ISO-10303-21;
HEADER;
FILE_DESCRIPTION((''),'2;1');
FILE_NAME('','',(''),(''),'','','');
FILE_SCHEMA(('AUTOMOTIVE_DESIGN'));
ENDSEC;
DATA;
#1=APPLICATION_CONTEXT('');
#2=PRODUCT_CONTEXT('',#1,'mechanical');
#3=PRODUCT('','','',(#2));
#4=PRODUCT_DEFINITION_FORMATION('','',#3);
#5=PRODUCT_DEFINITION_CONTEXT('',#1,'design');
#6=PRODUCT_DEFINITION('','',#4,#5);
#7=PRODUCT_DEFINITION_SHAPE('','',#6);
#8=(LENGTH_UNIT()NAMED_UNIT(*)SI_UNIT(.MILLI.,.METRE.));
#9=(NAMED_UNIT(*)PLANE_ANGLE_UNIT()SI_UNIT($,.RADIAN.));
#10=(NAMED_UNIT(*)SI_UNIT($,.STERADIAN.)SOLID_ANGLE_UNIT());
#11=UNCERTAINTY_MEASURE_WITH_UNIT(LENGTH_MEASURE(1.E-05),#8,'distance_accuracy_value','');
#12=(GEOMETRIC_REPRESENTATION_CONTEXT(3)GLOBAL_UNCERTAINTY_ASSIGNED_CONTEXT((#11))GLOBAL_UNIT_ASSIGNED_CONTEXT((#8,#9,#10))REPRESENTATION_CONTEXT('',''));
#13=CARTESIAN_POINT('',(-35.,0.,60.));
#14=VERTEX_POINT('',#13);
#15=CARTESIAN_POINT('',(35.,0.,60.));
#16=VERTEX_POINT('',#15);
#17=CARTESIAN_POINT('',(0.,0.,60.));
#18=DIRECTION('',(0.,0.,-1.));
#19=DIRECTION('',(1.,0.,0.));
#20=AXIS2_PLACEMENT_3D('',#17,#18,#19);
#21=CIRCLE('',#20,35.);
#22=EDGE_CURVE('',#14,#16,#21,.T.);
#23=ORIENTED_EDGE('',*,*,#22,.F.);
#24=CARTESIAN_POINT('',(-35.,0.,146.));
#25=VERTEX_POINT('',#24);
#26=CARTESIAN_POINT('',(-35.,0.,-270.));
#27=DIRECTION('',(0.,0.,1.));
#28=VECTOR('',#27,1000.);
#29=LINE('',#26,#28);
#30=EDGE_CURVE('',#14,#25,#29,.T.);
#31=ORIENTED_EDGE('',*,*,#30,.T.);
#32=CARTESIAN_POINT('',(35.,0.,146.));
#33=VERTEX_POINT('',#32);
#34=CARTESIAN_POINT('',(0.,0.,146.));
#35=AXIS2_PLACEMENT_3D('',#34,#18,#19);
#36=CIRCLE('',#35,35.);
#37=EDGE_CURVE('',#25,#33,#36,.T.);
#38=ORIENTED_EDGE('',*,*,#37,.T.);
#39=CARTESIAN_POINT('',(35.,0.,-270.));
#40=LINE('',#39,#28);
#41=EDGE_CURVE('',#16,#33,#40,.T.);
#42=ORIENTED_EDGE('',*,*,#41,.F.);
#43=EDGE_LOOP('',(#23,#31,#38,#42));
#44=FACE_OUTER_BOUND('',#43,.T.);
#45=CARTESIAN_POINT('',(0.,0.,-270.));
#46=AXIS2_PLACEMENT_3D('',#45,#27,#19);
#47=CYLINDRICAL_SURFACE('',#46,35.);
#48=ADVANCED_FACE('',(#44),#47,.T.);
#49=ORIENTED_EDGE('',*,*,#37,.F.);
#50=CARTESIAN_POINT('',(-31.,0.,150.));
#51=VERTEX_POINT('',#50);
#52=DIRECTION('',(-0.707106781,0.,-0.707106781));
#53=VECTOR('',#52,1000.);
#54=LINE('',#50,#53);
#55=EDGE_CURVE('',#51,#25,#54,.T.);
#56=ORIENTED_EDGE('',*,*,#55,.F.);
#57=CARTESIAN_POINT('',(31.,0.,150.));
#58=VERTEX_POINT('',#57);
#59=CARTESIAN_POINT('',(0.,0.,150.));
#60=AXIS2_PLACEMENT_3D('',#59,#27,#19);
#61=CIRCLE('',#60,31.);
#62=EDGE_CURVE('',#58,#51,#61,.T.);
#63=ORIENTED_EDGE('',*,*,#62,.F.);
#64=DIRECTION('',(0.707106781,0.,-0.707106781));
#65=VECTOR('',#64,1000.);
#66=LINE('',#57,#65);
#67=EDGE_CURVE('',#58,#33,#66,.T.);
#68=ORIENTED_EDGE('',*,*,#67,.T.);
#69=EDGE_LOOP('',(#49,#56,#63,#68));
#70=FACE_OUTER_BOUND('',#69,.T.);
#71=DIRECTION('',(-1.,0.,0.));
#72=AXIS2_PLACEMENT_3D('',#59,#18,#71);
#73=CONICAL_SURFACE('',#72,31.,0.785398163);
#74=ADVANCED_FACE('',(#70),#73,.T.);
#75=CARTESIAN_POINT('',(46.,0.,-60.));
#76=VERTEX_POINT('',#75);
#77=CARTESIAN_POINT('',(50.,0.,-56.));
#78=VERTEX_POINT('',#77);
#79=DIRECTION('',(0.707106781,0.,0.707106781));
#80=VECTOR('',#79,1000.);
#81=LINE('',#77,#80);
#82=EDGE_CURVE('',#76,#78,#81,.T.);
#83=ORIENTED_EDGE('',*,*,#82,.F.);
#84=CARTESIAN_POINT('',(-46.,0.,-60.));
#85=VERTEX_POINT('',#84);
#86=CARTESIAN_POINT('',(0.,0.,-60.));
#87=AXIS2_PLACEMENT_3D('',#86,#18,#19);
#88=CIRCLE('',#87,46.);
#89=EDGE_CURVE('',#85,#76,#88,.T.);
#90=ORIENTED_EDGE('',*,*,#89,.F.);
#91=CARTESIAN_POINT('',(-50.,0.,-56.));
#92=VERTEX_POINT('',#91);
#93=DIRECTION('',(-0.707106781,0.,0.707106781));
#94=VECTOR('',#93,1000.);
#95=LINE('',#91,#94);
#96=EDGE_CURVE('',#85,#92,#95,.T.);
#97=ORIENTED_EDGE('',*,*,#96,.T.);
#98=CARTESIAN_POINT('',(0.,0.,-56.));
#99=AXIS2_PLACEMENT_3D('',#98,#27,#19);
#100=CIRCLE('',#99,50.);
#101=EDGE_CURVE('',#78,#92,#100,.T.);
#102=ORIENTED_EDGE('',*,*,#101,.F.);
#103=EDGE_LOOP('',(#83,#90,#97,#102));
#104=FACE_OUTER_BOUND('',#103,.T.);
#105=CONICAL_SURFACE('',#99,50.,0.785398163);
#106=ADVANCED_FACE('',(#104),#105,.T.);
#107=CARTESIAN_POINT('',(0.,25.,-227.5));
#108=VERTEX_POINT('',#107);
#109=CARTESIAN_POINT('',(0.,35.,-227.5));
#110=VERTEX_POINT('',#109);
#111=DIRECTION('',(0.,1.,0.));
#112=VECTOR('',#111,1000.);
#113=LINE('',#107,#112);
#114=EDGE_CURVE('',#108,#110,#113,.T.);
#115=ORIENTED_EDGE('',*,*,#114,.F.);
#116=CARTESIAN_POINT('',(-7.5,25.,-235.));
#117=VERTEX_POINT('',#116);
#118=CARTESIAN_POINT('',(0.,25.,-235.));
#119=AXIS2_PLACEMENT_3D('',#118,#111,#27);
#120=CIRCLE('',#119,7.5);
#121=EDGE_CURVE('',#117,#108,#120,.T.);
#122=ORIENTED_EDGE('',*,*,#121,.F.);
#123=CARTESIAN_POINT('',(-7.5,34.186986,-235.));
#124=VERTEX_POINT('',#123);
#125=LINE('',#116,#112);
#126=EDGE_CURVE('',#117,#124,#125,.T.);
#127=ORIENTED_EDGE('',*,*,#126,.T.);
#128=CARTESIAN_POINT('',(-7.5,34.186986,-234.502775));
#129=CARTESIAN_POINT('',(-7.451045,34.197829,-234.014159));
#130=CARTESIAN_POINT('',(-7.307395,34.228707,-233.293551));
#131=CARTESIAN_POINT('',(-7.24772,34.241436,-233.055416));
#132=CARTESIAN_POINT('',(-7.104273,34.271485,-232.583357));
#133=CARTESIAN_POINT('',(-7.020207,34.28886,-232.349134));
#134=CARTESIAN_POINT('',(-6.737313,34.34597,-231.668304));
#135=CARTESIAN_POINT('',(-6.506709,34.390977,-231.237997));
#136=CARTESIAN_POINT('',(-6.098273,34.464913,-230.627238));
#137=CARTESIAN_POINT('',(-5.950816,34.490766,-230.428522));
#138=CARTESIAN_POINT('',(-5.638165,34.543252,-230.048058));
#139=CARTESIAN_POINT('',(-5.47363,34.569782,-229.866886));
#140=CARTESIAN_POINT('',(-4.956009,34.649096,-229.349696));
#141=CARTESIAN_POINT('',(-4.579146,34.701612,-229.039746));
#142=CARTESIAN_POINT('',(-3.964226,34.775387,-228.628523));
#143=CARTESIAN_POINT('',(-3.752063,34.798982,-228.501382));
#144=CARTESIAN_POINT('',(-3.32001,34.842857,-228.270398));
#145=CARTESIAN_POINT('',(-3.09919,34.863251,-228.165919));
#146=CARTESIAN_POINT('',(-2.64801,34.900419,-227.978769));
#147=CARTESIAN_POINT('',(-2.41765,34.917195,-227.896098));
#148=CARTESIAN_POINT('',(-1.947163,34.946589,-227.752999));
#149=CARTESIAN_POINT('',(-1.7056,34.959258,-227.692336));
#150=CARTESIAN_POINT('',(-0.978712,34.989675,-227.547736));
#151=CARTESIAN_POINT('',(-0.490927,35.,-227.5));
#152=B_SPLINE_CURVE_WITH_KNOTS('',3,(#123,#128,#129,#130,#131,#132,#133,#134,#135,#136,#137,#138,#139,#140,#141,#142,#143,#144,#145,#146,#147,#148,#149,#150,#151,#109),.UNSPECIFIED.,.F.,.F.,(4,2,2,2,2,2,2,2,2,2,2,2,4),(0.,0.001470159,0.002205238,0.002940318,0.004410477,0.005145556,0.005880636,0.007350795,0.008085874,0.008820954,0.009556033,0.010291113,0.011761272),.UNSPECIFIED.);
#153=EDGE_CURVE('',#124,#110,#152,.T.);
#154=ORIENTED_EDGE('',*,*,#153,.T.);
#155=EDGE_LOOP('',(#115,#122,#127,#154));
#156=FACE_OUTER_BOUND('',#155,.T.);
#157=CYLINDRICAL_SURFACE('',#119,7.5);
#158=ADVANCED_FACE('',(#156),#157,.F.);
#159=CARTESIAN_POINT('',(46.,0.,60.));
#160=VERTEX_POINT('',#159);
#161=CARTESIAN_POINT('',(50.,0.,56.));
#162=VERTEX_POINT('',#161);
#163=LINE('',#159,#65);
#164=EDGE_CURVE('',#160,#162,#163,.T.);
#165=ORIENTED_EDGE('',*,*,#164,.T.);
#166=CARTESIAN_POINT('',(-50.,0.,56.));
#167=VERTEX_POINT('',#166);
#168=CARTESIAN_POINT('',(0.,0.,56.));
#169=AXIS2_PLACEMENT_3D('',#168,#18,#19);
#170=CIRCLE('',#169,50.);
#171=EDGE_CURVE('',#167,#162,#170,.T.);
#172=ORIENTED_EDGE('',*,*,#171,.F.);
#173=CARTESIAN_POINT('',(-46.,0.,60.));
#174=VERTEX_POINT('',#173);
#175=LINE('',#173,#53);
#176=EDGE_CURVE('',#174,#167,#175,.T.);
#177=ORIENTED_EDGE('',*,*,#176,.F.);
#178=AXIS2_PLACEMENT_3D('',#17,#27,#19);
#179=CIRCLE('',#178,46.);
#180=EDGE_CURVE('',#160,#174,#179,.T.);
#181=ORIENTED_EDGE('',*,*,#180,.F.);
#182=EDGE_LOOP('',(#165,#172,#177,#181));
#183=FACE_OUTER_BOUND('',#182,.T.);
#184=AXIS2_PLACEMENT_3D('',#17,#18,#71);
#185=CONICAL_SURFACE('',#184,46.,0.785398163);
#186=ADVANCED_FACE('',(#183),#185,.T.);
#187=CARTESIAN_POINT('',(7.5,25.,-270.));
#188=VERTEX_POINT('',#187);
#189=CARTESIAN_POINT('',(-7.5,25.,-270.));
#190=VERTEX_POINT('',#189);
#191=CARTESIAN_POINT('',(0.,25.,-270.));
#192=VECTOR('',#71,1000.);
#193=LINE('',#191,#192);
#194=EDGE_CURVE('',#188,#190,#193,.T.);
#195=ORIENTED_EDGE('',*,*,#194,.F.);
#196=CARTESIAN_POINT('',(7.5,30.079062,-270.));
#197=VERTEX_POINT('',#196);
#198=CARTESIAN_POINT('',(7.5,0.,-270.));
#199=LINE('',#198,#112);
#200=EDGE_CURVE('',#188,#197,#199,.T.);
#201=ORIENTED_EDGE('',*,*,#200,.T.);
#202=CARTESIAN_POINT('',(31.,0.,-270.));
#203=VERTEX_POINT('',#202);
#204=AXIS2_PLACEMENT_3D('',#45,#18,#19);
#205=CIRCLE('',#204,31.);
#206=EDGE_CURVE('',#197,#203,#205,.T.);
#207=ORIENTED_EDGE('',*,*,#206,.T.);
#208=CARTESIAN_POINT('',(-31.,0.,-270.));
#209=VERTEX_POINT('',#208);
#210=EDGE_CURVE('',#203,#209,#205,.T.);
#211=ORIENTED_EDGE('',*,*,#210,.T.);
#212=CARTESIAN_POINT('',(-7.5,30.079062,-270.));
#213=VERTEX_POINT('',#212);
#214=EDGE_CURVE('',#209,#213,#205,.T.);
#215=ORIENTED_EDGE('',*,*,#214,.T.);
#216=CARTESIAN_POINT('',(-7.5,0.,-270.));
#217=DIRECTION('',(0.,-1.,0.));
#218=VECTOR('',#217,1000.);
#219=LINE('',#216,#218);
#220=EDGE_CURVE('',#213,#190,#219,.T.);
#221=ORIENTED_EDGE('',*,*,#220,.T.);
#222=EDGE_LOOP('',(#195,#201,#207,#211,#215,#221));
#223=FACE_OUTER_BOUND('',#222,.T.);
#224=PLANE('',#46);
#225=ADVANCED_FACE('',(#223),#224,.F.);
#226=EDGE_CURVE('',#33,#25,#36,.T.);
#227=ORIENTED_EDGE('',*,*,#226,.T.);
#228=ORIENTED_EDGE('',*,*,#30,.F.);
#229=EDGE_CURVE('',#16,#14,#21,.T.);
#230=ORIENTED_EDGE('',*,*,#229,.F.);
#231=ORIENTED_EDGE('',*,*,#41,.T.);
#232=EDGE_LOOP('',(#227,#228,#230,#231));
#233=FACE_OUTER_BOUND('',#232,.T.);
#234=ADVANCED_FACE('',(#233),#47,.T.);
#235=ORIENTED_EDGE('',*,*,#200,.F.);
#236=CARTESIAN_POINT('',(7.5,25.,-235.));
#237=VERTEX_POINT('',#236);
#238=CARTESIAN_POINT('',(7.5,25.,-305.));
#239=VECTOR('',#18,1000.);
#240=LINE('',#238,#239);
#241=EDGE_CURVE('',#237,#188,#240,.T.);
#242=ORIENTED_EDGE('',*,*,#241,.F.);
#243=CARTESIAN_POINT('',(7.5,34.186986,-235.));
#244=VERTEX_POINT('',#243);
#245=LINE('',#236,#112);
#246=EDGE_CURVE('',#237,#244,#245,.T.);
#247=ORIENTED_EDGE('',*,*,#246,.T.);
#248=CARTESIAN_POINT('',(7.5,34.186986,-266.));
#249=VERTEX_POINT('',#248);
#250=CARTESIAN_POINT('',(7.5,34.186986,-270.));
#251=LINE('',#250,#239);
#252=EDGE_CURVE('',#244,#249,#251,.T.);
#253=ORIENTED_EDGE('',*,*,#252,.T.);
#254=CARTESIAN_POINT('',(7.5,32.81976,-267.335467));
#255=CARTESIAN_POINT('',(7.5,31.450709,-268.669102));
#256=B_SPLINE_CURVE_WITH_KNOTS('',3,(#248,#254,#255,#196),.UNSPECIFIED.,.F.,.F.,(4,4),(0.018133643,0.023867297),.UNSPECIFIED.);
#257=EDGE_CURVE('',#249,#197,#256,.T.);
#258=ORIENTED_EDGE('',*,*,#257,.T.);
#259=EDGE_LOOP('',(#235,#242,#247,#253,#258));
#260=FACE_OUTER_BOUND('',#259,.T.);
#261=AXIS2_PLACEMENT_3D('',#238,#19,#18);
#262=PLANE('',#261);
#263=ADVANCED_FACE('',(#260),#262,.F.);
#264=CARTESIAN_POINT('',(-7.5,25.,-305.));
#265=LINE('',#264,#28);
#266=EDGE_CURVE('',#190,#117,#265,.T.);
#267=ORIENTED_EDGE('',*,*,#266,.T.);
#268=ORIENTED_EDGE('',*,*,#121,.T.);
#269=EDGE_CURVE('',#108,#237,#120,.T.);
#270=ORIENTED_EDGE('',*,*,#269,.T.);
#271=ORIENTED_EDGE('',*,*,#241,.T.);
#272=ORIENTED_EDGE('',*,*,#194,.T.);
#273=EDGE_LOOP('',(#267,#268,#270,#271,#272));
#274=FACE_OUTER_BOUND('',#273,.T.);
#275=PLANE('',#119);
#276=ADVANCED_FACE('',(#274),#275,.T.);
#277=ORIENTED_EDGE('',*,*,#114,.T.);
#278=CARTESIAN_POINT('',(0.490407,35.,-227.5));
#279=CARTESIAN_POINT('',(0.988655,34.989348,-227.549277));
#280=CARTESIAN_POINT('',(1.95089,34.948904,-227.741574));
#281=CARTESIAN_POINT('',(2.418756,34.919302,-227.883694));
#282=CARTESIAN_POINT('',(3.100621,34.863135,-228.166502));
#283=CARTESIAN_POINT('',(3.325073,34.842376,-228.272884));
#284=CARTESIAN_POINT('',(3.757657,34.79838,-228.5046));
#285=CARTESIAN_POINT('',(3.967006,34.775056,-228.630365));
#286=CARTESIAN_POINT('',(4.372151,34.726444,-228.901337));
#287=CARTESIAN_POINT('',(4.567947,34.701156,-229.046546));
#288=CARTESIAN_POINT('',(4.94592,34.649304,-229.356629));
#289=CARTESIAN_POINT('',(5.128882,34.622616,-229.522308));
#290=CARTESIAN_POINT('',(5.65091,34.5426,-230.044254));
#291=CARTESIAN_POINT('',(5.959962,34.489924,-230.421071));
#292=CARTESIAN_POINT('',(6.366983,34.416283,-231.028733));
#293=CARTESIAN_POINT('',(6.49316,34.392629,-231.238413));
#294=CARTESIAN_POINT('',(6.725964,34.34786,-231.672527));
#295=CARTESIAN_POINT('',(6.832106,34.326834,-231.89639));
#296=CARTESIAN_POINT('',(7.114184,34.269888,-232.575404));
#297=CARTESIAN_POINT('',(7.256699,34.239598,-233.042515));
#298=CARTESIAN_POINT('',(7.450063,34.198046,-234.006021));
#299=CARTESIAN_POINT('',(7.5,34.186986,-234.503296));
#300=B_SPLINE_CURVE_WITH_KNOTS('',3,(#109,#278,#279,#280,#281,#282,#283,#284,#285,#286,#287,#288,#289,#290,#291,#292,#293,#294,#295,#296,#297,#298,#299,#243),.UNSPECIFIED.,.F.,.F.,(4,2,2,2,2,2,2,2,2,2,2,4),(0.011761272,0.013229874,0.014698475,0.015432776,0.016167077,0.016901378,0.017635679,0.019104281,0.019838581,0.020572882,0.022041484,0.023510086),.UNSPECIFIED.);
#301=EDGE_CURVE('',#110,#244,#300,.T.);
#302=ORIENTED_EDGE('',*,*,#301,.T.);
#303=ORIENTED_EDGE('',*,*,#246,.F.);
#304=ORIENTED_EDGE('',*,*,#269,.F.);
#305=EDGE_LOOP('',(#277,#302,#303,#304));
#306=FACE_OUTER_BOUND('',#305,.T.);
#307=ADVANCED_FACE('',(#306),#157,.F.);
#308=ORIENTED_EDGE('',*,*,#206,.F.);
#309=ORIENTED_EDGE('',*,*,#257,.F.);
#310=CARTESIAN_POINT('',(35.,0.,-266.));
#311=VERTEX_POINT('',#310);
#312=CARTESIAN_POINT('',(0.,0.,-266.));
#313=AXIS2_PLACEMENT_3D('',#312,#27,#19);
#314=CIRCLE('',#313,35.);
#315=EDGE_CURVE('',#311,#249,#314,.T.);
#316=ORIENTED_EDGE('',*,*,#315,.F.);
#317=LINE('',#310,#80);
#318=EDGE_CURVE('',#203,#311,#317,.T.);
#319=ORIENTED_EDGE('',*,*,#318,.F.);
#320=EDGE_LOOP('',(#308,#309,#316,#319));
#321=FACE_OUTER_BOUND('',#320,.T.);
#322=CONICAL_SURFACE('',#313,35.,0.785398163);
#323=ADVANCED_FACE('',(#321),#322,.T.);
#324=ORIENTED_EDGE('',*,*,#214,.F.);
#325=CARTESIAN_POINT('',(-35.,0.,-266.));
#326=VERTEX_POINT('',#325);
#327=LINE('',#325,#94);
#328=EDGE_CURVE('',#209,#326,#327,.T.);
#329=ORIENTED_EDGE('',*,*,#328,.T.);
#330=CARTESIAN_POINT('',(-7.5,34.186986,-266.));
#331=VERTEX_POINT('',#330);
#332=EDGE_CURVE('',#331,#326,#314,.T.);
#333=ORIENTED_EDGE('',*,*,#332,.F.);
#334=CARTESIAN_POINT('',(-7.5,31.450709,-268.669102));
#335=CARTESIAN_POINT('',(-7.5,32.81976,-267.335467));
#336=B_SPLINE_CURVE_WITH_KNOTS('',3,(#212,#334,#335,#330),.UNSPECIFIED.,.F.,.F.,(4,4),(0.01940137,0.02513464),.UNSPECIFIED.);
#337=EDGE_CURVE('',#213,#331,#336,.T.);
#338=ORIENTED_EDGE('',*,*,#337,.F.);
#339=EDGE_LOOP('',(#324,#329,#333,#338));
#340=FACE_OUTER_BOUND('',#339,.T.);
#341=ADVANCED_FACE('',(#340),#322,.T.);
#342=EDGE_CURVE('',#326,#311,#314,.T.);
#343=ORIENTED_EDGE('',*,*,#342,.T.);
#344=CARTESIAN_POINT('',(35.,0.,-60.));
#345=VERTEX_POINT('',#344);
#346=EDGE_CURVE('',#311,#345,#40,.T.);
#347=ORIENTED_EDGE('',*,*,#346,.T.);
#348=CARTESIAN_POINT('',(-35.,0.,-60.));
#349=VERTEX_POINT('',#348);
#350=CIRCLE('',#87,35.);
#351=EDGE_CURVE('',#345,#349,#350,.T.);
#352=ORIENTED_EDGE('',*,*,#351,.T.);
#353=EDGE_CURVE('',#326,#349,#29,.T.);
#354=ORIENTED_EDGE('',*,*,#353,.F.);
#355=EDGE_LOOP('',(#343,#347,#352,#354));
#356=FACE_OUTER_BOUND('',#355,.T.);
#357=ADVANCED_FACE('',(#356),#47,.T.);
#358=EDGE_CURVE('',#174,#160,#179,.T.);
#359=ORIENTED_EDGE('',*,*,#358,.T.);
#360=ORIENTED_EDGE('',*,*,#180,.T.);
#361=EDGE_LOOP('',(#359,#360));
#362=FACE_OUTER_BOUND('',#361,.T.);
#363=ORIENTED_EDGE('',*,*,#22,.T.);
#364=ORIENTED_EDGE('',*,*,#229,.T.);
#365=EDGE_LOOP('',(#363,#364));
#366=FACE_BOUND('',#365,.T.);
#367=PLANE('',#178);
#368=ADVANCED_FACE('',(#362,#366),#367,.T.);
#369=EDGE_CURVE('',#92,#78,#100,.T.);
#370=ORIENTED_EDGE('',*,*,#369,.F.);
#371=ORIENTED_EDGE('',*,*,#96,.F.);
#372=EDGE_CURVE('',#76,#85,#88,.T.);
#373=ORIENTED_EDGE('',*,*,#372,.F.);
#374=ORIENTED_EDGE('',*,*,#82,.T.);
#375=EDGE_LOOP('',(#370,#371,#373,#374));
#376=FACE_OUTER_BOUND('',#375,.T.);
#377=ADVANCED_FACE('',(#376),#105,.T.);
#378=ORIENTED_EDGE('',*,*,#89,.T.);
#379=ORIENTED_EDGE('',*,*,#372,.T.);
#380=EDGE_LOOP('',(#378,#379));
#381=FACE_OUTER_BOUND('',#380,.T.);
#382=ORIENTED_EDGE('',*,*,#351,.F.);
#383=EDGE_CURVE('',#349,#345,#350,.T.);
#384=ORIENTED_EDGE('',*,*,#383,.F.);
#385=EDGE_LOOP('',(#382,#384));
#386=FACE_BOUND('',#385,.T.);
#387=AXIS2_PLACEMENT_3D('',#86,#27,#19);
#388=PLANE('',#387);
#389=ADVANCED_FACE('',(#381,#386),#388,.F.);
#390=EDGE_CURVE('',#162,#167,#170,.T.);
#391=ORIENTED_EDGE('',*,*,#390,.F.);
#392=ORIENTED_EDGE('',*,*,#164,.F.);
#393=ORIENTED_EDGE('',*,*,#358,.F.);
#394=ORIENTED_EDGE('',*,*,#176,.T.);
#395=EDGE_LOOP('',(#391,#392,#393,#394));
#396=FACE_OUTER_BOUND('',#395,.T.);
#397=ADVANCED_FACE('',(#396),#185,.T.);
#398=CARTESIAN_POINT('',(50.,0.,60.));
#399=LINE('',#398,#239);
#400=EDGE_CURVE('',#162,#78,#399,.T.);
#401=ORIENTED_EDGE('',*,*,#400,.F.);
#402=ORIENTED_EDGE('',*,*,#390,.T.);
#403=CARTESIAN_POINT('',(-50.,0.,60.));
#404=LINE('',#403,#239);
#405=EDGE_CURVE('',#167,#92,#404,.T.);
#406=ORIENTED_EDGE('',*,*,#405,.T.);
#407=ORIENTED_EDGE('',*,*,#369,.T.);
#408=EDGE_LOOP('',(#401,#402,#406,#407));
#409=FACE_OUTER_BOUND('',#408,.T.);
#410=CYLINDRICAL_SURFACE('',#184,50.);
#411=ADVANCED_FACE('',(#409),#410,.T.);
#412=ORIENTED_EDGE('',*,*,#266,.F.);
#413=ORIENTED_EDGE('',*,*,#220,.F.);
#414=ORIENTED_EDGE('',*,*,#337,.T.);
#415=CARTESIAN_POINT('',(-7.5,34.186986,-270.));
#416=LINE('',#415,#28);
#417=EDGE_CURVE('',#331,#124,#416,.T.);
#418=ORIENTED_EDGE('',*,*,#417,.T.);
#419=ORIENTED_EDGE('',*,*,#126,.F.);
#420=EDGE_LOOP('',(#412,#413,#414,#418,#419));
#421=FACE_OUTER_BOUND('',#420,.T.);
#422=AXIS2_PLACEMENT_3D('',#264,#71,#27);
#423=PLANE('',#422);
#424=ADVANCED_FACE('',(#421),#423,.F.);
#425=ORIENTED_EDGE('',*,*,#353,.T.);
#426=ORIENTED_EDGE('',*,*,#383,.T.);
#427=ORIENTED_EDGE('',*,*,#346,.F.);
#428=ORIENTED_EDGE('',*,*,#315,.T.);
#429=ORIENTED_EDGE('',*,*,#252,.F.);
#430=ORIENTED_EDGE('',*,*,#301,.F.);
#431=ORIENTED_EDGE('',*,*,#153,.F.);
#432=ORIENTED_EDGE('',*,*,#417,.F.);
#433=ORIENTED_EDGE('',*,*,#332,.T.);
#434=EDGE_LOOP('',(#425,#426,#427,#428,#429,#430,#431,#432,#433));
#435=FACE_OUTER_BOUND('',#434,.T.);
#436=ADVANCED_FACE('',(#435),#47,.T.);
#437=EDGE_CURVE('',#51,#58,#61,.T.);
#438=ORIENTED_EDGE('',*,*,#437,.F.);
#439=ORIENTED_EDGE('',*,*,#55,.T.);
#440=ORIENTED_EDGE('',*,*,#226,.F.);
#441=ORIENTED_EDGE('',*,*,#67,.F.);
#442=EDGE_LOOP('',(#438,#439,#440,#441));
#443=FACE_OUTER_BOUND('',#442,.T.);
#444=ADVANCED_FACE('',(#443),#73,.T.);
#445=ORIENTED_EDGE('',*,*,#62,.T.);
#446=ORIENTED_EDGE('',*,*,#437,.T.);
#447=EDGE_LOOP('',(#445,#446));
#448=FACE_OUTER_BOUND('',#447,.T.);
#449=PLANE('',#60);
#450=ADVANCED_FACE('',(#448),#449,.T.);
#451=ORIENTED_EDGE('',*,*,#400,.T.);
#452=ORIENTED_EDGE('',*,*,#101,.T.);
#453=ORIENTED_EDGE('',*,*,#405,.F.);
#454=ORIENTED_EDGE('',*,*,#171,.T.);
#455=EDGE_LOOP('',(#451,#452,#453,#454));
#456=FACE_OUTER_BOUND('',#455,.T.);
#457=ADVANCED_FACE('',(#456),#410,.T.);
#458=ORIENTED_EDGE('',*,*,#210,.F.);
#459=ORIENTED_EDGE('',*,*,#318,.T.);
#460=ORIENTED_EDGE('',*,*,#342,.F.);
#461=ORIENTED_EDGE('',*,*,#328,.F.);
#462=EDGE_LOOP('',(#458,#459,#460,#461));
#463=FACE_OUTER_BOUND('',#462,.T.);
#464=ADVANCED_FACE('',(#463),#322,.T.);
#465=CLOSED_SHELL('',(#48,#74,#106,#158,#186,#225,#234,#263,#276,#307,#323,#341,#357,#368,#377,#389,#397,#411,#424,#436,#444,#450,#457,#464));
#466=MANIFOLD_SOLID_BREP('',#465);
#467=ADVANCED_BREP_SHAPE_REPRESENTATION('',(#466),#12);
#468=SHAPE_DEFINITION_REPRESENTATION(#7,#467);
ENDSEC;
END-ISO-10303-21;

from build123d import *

# Parameters (mm, degrees)
BOSS_EXTRUDE1_DEPTH      = 150
BOSS_EXTRUDE1_DEPTH_BACK = 270
SKETCH1_R                = 35
SKETCH2_R                = 50
BOSS_EXTRUDE2_DEPTH      = 60
CHAMFER1_SIZE            = 4
CUT_EXTRUDE1_DEPTH       = 10


with BuildPart() as part:
    # Sketch1 → Boss-Extrude1 (new, two sides: drawn at the far end of the back side and taken through both)
    with BuildSketch(Plane.XY.offset(-BOSS_EXTRUDE1_DEPTH_BACK)):
        Circle(SKETCH1_R)
    extrude(amount=BOSS_EXTRUDE1_DEPTH + BOSS_EXTRUDE1_DEPTH_BACK)

    # Sketch2 → Boss-Extrude2 (add, symmetric)
    with BuildSketch(Plane.XY):
        Circle(SKETCH2_R)
    extrude(amount=BOSS_EXTRUDE2_DEPTH, both=True)

    # Chamfer1
    chamfer1_edges = [part.edges().sort_by_distance(p)[0] for p in [
        (-35, 0, -270),
        (-35, 0, 150),
        (-50, 0, -60),
        (-50, 0, 60),
    ]]
    chamfer(chamfer1_edges, length=CHAMFER1_SIZE)

    # Sketch3 → Cut-Extrude1 (cut)
    with BuildSketch(Plane(origin=(0, 35, 0), x_dir=(1, 0, 0), z_dir=(0, 1, 0))):
        with BuildLine():
            Line((-7.5, 305), (7.5, 305))
            Line((7.5, 305), (7.5, 235))
            ThreePointArc((7.5, 235), (0, 227.5), (-7.5, 235))
            Line((-7.5, 235), (-7.5, 305))
        make_face()
    extrude(amount=-CUT_EXTRUDE1_DEPTH, mode=Mode.SUBTRACT)


solid = part.part
